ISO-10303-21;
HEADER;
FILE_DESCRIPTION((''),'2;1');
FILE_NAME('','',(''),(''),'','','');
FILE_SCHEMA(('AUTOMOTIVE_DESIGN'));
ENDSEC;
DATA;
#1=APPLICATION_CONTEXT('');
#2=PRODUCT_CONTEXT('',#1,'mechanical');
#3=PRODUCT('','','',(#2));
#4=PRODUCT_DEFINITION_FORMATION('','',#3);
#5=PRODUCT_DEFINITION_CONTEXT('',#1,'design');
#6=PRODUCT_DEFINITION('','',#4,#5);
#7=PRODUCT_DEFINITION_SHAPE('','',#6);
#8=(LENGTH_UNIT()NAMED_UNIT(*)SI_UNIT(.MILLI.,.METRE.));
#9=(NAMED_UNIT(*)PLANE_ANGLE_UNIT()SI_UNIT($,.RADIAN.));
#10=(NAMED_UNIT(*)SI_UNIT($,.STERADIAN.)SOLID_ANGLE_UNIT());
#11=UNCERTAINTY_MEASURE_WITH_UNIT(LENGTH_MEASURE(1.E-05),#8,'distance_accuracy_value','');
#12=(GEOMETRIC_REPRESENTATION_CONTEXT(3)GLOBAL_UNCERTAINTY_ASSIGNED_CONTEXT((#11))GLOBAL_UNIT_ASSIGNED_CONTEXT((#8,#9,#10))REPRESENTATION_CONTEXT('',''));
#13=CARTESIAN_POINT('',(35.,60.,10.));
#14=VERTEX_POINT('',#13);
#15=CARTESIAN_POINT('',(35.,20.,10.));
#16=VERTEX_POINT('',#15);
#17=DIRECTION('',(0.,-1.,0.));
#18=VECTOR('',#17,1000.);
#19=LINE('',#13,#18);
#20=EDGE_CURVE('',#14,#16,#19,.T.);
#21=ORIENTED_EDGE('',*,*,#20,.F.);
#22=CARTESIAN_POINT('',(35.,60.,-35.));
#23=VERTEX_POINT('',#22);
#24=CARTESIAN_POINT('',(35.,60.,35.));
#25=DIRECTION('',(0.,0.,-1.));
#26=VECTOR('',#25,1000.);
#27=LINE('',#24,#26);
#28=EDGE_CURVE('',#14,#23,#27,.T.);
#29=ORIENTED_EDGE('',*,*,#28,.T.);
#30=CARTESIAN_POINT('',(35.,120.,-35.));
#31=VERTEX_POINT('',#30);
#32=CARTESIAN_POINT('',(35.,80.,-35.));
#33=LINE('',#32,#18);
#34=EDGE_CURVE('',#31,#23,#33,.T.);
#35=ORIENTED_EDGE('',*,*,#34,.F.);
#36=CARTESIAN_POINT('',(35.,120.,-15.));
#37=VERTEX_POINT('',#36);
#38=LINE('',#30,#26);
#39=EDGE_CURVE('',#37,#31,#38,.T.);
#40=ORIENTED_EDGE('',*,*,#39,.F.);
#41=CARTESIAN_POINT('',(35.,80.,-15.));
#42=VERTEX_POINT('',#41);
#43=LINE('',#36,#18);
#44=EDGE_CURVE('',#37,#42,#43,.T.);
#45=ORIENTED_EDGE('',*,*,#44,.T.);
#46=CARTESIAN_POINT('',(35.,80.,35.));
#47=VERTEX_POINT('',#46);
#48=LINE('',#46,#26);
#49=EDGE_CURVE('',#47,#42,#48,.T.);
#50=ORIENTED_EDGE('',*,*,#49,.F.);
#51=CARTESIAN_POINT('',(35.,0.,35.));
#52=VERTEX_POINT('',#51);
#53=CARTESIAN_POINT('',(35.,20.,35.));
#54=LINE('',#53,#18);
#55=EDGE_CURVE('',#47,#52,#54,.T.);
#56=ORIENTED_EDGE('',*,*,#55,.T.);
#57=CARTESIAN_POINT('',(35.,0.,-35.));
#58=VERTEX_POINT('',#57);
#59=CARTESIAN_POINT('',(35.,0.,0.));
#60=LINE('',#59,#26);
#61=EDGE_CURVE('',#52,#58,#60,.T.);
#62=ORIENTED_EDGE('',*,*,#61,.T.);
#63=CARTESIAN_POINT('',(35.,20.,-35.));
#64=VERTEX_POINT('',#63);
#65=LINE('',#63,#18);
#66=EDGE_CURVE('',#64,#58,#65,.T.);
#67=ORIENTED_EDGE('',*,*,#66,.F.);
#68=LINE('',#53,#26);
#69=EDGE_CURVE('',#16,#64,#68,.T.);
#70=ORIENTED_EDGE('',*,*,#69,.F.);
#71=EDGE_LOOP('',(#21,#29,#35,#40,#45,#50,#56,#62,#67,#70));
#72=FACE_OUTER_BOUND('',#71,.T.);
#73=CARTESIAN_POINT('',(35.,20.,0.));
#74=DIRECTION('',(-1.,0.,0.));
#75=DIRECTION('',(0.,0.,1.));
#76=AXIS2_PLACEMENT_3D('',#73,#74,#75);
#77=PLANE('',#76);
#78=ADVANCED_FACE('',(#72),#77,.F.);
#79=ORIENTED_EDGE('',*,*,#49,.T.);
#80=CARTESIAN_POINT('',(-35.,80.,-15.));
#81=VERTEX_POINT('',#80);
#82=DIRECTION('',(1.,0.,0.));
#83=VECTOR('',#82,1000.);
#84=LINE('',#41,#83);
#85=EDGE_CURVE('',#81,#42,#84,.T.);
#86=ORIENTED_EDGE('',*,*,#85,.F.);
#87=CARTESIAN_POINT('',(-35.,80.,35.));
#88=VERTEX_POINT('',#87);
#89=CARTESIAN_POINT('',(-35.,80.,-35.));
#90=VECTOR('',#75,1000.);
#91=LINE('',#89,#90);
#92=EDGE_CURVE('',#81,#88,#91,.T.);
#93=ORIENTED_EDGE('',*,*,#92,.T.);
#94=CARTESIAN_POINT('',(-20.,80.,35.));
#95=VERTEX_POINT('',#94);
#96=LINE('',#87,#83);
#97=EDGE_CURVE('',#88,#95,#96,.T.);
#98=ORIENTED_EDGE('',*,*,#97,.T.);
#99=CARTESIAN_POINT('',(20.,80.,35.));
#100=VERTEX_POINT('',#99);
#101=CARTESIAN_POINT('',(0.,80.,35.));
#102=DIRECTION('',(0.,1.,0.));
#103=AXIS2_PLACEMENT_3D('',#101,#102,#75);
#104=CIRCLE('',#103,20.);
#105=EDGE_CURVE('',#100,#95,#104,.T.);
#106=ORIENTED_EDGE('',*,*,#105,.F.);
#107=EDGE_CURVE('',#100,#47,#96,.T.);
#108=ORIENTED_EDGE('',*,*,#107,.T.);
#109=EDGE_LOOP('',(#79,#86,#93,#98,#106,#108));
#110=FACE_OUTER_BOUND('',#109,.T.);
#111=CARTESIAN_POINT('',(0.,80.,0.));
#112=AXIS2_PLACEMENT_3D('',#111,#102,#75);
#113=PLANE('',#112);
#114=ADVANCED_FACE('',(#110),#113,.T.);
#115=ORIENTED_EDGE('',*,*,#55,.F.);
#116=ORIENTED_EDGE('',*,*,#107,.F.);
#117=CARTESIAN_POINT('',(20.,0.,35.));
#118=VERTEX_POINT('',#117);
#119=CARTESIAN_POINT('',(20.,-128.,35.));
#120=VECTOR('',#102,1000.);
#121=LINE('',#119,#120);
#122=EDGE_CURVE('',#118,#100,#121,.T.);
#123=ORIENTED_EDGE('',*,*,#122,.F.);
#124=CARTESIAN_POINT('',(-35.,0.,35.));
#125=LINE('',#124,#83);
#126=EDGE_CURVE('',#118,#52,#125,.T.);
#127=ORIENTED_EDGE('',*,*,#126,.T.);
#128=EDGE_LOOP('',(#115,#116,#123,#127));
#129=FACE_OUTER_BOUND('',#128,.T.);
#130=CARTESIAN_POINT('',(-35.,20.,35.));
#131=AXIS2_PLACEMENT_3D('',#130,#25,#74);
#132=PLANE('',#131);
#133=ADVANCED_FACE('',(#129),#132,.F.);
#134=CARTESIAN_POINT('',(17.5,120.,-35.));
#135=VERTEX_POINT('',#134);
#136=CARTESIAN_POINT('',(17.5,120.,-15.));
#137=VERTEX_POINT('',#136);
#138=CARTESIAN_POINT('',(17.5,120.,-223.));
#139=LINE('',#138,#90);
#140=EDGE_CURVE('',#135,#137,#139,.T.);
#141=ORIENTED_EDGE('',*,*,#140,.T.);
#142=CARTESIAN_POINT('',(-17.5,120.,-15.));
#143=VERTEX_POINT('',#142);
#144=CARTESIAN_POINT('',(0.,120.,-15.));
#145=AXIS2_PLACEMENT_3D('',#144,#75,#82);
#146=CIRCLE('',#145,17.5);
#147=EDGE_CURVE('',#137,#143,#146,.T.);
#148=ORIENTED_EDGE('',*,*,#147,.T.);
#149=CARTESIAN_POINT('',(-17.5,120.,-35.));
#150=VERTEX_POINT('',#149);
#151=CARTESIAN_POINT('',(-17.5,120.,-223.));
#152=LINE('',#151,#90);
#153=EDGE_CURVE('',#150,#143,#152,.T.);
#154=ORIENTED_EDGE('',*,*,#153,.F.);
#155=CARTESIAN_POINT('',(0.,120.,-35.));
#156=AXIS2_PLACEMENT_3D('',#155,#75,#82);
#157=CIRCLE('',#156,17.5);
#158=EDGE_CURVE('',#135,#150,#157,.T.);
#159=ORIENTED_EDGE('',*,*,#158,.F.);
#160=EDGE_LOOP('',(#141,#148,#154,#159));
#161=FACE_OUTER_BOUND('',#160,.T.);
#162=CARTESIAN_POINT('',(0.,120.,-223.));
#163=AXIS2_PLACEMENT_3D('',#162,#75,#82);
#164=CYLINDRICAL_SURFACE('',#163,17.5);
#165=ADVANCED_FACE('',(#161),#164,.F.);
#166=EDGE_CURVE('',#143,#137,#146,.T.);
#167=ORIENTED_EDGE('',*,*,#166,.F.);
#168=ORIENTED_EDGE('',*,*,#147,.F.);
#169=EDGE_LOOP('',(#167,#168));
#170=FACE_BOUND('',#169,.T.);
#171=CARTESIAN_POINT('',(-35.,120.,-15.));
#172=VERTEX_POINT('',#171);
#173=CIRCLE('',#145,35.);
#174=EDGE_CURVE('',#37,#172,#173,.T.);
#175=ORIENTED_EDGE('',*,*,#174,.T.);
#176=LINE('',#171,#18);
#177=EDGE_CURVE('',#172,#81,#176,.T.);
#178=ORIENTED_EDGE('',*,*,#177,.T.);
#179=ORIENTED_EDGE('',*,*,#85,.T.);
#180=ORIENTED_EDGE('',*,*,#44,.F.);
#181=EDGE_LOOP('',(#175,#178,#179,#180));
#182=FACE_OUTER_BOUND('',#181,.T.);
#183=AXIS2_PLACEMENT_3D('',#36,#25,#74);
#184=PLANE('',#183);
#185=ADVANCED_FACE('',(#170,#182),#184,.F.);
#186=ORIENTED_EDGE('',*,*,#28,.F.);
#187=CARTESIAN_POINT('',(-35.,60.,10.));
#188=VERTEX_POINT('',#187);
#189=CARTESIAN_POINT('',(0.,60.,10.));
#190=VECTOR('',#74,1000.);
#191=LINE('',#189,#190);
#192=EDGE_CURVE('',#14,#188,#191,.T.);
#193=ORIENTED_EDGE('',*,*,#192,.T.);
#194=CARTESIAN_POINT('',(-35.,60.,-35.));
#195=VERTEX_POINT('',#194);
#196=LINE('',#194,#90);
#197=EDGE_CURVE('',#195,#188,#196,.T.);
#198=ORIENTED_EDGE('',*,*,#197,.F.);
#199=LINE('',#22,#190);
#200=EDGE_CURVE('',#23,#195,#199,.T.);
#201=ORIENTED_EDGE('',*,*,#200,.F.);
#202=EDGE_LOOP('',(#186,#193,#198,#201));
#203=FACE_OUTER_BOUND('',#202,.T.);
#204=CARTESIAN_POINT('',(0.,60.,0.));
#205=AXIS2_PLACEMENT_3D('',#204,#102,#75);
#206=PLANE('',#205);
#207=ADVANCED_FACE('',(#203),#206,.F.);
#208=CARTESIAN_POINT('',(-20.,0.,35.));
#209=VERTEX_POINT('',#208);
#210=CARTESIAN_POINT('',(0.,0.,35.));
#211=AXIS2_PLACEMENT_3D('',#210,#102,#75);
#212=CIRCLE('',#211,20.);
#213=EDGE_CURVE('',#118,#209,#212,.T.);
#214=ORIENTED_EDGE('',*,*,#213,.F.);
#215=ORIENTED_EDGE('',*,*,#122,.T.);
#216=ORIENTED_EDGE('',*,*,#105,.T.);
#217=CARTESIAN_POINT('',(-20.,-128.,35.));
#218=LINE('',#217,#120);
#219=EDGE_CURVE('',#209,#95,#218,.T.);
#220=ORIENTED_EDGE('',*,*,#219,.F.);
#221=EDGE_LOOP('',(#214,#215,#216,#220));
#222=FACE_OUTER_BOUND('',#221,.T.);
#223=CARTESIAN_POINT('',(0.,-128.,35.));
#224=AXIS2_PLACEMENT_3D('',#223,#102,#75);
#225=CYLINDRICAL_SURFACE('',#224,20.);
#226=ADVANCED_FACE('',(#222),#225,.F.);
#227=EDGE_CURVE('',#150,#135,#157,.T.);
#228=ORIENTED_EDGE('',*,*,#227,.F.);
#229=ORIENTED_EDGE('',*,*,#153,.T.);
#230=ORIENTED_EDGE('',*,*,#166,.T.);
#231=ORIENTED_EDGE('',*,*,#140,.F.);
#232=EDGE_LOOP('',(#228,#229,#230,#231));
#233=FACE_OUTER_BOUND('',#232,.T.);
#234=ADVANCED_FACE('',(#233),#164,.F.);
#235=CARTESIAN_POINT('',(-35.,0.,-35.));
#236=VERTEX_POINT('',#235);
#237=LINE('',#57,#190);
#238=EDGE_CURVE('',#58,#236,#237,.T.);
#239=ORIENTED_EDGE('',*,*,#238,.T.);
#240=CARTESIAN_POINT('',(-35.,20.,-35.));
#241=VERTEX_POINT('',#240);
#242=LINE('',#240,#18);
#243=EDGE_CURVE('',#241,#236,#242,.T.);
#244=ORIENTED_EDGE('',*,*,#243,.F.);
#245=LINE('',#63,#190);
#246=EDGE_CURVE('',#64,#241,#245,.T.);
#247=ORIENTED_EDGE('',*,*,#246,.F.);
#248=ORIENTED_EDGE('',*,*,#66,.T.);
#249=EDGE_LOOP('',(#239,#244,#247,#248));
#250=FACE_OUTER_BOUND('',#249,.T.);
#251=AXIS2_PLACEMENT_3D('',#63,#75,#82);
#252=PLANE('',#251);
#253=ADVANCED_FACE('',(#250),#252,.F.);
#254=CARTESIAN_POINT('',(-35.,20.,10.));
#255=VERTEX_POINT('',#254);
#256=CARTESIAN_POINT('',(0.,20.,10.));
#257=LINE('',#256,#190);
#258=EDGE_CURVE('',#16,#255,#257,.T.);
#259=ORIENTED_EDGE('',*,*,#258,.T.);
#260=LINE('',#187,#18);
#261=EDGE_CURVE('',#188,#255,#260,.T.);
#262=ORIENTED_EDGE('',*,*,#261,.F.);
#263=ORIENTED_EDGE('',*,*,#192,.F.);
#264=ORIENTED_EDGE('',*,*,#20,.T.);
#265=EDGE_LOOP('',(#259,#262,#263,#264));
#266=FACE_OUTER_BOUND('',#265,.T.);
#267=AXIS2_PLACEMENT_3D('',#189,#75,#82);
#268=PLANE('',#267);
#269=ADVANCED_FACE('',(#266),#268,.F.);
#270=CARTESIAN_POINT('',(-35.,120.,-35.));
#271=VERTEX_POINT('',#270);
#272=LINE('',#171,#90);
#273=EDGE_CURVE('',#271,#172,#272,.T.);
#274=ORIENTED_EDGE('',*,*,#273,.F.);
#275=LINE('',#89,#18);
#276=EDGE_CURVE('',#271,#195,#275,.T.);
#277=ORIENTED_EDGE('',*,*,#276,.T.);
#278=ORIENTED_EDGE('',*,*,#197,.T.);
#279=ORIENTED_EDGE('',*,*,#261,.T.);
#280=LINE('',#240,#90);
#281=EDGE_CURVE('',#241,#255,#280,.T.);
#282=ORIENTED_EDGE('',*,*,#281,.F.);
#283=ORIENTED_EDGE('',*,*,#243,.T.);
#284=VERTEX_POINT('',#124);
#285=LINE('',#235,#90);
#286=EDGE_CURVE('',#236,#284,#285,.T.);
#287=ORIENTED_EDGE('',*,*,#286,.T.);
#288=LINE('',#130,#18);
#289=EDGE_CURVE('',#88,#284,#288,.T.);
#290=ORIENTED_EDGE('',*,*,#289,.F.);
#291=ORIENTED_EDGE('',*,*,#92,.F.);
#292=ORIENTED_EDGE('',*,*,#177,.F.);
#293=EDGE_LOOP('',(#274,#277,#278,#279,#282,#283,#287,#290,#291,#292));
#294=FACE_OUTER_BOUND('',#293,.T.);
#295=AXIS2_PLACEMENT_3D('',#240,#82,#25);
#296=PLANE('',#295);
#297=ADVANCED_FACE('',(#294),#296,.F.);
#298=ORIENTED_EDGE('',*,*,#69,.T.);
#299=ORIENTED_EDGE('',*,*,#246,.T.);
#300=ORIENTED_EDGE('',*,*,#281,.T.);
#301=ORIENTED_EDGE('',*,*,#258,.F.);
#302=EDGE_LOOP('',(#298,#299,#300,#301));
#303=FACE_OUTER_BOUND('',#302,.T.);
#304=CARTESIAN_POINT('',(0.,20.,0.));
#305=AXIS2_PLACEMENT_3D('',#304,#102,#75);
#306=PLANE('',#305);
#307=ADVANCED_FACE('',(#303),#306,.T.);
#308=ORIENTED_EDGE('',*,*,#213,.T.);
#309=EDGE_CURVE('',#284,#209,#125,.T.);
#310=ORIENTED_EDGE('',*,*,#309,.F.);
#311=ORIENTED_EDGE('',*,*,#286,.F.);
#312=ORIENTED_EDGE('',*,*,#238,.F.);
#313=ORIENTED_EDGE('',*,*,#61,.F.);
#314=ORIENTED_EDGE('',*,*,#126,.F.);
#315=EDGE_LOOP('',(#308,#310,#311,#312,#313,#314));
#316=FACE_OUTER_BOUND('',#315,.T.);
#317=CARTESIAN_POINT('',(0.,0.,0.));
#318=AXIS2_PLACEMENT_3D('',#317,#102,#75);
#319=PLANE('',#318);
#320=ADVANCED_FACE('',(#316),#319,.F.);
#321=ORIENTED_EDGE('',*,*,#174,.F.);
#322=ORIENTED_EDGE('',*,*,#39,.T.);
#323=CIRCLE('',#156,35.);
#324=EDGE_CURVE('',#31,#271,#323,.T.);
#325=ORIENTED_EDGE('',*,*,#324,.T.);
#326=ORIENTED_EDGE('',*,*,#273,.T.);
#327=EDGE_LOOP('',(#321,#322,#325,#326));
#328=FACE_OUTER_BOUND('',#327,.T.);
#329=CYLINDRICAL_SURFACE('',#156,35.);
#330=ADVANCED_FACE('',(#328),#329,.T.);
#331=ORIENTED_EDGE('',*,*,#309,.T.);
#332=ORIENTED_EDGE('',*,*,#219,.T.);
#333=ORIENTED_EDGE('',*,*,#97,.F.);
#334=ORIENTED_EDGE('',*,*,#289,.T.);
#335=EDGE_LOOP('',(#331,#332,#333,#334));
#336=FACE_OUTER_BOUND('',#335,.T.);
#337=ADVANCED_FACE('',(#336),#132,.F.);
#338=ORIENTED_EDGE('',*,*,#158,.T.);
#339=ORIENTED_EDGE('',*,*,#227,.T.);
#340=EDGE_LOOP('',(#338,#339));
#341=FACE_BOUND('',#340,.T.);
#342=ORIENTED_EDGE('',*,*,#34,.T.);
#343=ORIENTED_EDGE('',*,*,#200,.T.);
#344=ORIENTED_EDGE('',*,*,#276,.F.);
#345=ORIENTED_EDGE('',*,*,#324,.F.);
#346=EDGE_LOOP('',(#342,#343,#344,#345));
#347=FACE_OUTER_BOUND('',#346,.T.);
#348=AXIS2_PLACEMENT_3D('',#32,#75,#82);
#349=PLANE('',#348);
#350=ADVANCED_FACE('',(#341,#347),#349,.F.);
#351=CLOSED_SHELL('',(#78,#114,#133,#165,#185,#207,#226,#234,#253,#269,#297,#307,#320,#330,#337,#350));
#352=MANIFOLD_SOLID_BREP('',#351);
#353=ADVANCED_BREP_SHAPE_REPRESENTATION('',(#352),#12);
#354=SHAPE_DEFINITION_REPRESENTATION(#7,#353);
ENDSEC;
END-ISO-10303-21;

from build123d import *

# Parameters (mm, degrees)
BASE_BLOCK_DEPTH        = 20
BODY_PROFILE_W          = 70
BODY_PROFILE_H          = 25
BODY_SECTION_DEPTH      = 40
SHELF_PROFILE_W         = 70
SHELF_PROFILE_H         = 70
SHELF_BLOCK_DEPTH       = 20
UPRIGHT_PROFILE_W       = 70
UPRIGHT_PROFILE_H       = 20
UPRIGHT_WALL_DEPTH      = 40
ROUNDED_LUG_DEPTH       = 20
LUG_HOLE_PROFILE_R      = 17.5
LUG_THROUGH_HOLE_DEPTH  = 208
HALF_BEARING_BORE_DEPTH = 208


with BuildPart() as part:
    # Base Profile → Base Block (new body)
    with BuildSketch(Plane(origin=(0, 0, 0), x_dir=(1, 0, 0), z_dir=(0, 1, 0))):
        Polygon((35, 0), (35, 35), (-35, 35), (-35, -35), (35, -35), align=None)
    extrude(amount=BASE_BLOCK_DEPTH)

    # Body Profile → Body Section (add)
    with BuildSketch(Plane(origin=(0, 20, 0), x_dir=(1, 0, 0), z_dir=(0, 1, 0))):
        with Locations((0, -22.5)):
            Rectangle(BODY_PROFILE_W, BODY_PROFILE_H)
    extrude(amount=BODY_SECTION_DEPTH)

    # Shelf Profile → Shelf Block (add)
    with BuildSketch(Plane(origin=(0, 60, 0), x_dir=(1, 0, 0), z_dir=(0, 1, 0))):
        Rectangle(SHELF_PROFILE_W, SHELF_PROFILE_H)
    extrude(amount=SHELF_BLOCK_DEPTH)

    # Upright Profile → Upright Wall (add)
    with BuildSketch(Plane(origin=(0, 80, 0), x_dir=(1, 0, 0), z_dir=(0, 1, 0))):
        with Locations((0, 25)):
            Rectangle(UPRIGHT_PROFILE_W, UPRIGHT_PROFILE_H)
    extrude(amount=UPRIGHT_WALL_DEPTH)

    # Lug Profile → Rounded Lug (add)
    with BuildSketch(Plane.XY.offset(-15)):
        with BuildLine():
            Line((-35, 120), (35, 120))
            ThreePointArc((35, 120), (0, 155), (-35, 120))
        make_face()
    extrude(amount=-ROUNDED_LUG_DEPTH)

    # Lug Hole Profile → Lug Through Hole (cut)
    with BuildSketch(Plane.XY.offset(-15)):
        with Locations((0, 120)):
            Circle(LUG_HOLE_PROFILE_R)
    extrude(amount=-LUG_THROUGH_HOLE_DEPTH, mode=Mode.SUBTRACT)

    # Bearing Bore Profile → Half Bearing Bore (cut)
    with BuildSketch(Plane(origin=(0, 80, 0), x_dir=(1, 0, 0), z_dir=(0, 1, 0))):
        with BuildLine():
            Line((-20, -35), (20, -35))
            ThreePointArc((20, -35), (0, -15), (-20, -35))
        make_face()
    extrude(amount=-HALF_BEARING_BORE_DEPTH, mode=Mode.SUBTRACT)


solid = part.part
